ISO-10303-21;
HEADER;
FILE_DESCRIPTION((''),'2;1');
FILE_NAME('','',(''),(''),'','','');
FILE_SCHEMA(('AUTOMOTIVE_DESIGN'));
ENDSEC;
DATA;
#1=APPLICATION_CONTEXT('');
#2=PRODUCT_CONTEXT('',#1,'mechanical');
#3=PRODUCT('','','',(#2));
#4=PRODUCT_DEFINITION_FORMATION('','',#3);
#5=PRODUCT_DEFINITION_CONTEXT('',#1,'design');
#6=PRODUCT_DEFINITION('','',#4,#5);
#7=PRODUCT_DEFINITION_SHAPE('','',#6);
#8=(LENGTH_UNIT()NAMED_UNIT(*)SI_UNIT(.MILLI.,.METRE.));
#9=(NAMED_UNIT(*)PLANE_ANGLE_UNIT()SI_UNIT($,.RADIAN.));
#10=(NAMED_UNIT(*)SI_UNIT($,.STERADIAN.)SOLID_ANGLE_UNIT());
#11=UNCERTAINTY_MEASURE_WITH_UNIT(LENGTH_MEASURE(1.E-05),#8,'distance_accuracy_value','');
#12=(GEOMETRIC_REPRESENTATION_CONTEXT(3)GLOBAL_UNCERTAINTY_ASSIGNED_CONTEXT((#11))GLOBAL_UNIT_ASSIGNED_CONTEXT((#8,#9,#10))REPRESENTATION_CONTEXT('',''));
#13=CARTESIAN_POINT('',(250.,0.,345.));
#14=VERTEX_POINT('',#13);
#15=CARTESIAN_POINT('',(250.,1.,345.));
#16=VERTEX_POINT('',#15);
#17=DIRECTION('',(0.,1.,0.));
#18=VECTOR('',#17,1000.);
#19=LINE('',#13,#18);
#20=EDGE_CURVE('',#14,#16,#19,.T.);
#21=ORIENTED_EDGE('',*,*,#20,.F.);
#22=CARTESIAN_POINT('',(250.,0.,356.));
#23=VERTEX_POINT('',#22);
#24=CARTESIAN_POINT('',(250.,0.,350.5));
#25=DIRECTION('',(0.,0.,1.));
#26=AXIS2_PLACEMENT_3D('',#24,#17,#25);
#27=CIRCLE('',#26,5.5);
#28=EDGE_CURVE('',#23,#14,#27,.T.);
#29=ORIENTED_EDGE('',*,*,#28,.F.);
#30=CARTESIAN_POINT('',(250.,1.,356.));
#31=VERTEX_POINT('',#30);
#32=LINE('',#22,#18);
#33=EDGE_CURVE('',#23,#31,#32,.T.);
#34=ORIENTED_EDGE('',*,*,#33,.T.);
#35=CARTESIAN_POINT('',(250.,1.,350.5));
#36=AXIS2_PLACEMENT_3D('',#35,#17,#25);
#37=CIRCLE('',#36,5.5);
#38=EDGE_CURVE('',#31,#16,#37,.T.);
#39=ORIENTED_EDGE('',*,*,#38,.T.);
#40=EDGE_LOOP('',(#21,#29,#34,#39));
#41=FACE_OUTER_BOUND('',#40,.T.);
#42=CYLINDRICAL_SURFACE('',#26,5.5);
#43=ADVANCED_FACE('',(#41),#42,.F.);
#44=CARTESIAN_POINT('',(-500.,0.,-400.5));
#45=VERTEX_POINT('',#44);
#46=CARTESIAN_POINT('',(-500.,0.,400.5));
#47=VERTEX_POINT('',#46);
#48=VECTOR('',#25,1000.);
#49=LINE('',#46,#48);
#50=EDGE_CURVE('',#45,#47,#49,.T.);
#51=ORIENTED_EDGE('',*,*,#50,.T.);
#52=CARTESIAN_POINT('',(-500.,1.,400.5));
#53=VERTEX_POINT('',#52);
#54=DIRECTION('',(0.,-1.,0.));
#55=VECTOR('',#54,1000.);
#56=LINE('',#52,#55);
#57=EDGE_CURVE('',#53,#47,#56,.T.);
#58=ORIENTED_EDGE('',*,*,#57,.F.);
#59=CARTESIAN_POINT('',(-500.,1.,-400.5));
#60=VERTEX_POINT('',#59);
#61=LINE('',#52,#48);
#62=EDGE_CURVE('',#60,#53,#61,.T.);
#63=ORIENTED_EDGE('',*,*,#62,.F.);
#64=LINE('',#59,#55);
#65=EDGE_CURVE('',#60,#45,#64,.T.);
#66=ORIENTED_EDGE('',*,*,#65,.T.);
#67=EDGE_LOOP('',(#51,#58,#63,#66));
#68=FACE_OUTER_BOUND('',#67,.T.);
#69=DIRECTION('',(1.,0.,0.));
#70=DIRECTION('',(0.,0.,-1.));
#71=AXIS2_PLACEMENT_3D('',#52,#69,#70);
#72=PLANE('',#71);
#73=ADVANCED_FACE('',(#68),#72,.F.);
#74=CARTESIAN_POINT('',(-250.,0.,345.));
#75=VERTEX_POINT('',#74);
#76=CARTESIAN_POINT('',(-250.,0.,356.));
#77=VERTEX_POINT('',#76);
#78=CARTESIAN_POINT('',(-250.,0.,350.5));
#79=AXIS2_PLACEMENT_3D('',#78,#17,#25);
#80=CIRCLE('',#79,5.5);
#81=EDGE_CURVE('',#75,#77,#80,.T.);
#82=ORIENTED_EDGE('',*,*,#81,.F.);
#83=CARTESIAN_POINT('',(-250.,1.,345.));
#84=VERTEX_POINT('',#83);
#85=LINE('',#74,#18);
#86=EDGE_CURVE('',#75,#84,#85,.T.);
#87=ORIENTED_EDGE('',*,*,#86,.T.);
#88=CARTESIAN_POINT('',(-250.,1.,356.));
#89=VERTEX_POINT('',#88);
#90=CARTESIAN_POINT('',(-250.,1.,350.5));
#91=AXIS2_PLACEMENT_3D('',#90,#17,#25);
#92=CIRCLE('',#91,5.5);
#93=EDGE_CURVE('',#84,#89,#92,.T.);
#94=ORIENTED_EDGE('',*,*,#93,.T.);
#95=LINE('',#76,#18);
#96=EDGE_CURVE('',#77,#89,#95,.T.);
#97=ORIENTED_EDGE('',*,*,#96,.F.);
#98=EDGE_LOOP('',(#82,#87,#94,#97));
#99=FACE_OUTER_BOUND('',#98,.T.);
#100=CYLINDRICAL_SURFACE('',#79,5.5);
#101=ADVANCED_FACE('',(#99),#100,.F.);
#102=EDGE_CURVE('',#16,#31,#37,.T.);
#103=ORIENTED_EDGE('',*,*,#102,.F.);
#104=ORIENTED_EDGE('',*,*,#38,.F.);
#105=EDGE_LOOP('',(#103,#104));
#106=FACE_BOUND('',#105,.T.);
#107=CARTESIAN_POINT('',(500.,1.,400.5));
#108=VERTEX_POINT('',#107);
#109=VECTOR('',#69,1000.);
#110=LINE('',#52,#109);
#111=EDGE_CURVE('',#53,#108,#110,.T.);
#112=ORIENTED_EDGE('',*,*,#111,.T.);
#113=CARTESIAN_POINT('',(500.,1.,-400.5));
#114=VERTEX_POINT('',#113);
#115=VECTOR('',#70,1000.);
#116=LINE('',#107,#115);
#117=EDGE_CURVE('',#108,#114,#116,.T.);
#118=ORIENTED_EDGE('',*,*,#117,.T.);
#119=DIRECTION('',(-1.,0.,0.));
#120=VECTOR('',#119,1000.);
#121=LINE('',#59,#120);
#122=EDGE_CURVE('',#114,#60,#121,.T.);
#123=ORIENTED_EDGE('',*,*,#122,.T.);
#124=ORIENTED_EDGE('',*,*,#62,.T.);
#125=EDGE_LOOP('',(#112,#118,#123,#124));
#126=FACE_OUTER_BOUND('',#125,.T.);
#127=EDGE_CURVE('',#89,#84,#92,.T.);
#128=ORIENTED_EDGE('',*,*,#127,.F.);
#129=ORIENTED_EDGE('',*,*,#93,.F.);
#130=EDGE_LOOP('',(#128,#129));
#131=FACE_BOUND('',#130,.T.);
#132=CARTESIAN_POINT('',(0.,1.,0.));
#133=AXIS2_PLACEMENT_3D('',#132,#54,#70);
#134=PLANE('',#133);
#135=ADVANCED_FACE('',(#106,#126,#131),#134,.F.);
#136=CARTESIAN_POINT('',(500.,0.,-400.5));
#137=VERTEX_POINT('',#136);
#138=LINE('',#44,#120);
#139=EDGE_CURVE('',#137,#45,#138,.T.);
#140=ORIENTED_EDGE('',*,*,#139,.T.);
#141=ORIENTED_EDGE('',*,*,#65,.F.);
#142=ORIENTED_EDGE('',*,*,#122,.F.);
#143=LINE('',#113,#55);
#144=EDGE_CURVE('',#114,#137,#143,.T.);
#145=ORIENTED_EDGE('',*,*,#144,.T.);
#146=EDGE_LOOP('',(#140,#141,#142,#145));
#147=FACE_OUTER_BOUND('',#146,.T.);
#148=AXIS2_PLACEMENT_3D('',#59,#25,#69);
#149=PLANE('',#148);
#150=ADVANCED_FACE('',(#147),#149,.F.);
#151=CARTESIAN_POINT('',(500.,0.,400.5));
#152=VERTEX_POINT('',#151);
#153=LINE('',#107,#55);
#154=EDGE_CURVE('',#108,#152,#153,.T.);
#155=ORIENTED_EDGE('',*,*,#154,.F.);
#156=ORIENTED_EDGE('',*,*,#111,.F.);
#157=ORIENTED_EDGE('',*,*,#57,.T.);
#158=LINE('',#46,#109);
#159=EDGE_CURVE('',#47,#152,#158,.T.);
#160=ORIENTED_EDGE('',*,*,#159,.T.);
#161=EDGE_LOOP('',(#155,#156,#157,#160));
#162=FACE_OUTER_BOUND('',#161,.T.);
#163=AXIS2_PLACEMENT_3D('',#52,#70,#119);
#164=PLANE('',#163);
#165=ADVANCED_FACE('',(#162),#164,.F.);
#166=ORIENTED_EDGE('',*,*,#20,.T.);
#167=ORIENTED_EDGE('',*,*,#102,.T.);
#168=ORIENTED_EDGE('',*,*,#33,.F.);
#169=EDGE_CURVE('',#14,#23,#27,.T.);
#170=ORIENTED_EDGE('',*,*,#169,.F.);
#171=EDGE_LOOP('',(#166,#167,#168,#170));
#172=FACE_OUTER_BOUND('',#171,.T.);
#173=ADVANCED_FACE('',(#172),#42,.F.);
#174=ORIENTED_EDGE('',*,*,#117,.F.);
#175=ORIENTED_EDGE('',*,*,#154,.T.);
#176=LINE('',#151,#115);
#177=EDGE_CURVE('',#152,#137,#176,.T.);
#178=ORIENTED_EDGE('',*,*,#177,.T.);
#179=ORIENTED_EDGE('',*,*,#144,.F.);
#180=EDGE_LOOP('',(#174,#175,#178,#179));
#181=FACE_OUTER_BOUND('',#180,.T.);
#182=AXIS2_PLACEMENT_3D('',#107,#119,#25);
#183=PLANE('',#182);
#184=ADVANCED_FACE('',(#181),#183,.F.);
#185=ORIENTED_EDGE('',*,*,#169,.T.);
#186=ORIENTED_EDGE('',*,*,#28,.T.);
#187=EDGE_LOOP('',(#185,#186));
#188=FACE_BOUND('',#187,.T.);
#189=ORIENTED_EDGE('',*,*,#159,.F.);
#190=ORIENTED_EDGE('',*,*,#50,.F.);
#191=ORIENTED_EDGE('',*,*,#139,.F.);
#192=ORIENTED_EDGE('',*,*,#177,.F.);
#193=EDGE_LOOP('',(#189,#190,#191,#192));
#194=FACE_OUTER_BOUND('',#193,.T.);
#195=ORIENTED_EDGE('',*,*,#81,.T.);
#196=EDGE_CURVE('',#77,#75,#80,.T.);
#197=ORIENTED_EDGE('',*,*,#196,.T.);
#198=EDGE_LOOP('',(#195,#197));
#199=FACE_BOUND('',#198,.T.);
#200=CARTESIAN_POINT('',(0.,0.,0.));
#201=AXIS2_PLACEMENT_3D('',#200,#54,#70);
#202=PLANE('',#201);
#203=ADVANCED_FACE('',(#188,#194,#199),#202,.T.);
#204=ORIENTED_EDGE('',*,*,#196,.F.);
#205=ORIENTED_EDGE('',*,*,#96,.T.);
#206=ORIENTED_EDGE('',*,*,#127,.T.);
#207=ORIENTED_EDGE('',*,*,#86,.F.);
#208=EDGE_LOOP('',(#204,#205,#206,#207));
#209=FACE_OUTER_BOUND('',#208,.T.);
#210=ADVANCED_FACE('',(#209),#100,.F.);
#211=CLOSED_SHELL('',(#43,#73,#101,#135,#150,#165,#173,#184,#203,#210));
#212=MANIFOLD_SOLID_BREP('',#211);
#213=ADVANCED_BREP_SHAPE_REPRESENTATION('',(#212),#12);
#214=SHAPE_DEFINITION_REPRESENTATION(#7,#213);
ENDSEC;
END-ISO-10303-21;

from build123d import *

# Parameters (mm, degrees)
SKETCH1_W           = 1000
SKETCH1_H           = 801
BOSS_EXTRUDE1_DEPTH = 1
SKETCH2_R           = 5.5
CUT_EXTRUDE1_DEPTH  = 641.625670731


with BuildPart() as part:
    # Sketch1 → Boss-Extrude1 (new body)
    with BuildSketch(Plane(origin=(0, 0, 0), x_dir=(1, 0, 0), z_dir=(0, 1, 0))):
        Rectangle(SKETCH1_W, SKETCH1_H)
    extrude(amount=BOSS_EXTRUDE1_DEPTH)

    # Sketch2 → Cut-Extrude1 (cut, through all)
    with BuildSketch(Plane(origin=(0, 1, 0), x_dir=(1, 0, 0), z_dir=(0, 1, 0))):
        with Locations(Location((-250, -350.5, 0), (0, 0, 270))):
            Circle(SKETCH2_R)
        with Locations(Location((250, -350.5, 0), (0, 0, 270))):
            Circle(SKETCH2_R)
    extrude(amount=-CUT_EXTRUDE1_DEPTH, mode=Mode.SUBTRACT)


solid = part.part
